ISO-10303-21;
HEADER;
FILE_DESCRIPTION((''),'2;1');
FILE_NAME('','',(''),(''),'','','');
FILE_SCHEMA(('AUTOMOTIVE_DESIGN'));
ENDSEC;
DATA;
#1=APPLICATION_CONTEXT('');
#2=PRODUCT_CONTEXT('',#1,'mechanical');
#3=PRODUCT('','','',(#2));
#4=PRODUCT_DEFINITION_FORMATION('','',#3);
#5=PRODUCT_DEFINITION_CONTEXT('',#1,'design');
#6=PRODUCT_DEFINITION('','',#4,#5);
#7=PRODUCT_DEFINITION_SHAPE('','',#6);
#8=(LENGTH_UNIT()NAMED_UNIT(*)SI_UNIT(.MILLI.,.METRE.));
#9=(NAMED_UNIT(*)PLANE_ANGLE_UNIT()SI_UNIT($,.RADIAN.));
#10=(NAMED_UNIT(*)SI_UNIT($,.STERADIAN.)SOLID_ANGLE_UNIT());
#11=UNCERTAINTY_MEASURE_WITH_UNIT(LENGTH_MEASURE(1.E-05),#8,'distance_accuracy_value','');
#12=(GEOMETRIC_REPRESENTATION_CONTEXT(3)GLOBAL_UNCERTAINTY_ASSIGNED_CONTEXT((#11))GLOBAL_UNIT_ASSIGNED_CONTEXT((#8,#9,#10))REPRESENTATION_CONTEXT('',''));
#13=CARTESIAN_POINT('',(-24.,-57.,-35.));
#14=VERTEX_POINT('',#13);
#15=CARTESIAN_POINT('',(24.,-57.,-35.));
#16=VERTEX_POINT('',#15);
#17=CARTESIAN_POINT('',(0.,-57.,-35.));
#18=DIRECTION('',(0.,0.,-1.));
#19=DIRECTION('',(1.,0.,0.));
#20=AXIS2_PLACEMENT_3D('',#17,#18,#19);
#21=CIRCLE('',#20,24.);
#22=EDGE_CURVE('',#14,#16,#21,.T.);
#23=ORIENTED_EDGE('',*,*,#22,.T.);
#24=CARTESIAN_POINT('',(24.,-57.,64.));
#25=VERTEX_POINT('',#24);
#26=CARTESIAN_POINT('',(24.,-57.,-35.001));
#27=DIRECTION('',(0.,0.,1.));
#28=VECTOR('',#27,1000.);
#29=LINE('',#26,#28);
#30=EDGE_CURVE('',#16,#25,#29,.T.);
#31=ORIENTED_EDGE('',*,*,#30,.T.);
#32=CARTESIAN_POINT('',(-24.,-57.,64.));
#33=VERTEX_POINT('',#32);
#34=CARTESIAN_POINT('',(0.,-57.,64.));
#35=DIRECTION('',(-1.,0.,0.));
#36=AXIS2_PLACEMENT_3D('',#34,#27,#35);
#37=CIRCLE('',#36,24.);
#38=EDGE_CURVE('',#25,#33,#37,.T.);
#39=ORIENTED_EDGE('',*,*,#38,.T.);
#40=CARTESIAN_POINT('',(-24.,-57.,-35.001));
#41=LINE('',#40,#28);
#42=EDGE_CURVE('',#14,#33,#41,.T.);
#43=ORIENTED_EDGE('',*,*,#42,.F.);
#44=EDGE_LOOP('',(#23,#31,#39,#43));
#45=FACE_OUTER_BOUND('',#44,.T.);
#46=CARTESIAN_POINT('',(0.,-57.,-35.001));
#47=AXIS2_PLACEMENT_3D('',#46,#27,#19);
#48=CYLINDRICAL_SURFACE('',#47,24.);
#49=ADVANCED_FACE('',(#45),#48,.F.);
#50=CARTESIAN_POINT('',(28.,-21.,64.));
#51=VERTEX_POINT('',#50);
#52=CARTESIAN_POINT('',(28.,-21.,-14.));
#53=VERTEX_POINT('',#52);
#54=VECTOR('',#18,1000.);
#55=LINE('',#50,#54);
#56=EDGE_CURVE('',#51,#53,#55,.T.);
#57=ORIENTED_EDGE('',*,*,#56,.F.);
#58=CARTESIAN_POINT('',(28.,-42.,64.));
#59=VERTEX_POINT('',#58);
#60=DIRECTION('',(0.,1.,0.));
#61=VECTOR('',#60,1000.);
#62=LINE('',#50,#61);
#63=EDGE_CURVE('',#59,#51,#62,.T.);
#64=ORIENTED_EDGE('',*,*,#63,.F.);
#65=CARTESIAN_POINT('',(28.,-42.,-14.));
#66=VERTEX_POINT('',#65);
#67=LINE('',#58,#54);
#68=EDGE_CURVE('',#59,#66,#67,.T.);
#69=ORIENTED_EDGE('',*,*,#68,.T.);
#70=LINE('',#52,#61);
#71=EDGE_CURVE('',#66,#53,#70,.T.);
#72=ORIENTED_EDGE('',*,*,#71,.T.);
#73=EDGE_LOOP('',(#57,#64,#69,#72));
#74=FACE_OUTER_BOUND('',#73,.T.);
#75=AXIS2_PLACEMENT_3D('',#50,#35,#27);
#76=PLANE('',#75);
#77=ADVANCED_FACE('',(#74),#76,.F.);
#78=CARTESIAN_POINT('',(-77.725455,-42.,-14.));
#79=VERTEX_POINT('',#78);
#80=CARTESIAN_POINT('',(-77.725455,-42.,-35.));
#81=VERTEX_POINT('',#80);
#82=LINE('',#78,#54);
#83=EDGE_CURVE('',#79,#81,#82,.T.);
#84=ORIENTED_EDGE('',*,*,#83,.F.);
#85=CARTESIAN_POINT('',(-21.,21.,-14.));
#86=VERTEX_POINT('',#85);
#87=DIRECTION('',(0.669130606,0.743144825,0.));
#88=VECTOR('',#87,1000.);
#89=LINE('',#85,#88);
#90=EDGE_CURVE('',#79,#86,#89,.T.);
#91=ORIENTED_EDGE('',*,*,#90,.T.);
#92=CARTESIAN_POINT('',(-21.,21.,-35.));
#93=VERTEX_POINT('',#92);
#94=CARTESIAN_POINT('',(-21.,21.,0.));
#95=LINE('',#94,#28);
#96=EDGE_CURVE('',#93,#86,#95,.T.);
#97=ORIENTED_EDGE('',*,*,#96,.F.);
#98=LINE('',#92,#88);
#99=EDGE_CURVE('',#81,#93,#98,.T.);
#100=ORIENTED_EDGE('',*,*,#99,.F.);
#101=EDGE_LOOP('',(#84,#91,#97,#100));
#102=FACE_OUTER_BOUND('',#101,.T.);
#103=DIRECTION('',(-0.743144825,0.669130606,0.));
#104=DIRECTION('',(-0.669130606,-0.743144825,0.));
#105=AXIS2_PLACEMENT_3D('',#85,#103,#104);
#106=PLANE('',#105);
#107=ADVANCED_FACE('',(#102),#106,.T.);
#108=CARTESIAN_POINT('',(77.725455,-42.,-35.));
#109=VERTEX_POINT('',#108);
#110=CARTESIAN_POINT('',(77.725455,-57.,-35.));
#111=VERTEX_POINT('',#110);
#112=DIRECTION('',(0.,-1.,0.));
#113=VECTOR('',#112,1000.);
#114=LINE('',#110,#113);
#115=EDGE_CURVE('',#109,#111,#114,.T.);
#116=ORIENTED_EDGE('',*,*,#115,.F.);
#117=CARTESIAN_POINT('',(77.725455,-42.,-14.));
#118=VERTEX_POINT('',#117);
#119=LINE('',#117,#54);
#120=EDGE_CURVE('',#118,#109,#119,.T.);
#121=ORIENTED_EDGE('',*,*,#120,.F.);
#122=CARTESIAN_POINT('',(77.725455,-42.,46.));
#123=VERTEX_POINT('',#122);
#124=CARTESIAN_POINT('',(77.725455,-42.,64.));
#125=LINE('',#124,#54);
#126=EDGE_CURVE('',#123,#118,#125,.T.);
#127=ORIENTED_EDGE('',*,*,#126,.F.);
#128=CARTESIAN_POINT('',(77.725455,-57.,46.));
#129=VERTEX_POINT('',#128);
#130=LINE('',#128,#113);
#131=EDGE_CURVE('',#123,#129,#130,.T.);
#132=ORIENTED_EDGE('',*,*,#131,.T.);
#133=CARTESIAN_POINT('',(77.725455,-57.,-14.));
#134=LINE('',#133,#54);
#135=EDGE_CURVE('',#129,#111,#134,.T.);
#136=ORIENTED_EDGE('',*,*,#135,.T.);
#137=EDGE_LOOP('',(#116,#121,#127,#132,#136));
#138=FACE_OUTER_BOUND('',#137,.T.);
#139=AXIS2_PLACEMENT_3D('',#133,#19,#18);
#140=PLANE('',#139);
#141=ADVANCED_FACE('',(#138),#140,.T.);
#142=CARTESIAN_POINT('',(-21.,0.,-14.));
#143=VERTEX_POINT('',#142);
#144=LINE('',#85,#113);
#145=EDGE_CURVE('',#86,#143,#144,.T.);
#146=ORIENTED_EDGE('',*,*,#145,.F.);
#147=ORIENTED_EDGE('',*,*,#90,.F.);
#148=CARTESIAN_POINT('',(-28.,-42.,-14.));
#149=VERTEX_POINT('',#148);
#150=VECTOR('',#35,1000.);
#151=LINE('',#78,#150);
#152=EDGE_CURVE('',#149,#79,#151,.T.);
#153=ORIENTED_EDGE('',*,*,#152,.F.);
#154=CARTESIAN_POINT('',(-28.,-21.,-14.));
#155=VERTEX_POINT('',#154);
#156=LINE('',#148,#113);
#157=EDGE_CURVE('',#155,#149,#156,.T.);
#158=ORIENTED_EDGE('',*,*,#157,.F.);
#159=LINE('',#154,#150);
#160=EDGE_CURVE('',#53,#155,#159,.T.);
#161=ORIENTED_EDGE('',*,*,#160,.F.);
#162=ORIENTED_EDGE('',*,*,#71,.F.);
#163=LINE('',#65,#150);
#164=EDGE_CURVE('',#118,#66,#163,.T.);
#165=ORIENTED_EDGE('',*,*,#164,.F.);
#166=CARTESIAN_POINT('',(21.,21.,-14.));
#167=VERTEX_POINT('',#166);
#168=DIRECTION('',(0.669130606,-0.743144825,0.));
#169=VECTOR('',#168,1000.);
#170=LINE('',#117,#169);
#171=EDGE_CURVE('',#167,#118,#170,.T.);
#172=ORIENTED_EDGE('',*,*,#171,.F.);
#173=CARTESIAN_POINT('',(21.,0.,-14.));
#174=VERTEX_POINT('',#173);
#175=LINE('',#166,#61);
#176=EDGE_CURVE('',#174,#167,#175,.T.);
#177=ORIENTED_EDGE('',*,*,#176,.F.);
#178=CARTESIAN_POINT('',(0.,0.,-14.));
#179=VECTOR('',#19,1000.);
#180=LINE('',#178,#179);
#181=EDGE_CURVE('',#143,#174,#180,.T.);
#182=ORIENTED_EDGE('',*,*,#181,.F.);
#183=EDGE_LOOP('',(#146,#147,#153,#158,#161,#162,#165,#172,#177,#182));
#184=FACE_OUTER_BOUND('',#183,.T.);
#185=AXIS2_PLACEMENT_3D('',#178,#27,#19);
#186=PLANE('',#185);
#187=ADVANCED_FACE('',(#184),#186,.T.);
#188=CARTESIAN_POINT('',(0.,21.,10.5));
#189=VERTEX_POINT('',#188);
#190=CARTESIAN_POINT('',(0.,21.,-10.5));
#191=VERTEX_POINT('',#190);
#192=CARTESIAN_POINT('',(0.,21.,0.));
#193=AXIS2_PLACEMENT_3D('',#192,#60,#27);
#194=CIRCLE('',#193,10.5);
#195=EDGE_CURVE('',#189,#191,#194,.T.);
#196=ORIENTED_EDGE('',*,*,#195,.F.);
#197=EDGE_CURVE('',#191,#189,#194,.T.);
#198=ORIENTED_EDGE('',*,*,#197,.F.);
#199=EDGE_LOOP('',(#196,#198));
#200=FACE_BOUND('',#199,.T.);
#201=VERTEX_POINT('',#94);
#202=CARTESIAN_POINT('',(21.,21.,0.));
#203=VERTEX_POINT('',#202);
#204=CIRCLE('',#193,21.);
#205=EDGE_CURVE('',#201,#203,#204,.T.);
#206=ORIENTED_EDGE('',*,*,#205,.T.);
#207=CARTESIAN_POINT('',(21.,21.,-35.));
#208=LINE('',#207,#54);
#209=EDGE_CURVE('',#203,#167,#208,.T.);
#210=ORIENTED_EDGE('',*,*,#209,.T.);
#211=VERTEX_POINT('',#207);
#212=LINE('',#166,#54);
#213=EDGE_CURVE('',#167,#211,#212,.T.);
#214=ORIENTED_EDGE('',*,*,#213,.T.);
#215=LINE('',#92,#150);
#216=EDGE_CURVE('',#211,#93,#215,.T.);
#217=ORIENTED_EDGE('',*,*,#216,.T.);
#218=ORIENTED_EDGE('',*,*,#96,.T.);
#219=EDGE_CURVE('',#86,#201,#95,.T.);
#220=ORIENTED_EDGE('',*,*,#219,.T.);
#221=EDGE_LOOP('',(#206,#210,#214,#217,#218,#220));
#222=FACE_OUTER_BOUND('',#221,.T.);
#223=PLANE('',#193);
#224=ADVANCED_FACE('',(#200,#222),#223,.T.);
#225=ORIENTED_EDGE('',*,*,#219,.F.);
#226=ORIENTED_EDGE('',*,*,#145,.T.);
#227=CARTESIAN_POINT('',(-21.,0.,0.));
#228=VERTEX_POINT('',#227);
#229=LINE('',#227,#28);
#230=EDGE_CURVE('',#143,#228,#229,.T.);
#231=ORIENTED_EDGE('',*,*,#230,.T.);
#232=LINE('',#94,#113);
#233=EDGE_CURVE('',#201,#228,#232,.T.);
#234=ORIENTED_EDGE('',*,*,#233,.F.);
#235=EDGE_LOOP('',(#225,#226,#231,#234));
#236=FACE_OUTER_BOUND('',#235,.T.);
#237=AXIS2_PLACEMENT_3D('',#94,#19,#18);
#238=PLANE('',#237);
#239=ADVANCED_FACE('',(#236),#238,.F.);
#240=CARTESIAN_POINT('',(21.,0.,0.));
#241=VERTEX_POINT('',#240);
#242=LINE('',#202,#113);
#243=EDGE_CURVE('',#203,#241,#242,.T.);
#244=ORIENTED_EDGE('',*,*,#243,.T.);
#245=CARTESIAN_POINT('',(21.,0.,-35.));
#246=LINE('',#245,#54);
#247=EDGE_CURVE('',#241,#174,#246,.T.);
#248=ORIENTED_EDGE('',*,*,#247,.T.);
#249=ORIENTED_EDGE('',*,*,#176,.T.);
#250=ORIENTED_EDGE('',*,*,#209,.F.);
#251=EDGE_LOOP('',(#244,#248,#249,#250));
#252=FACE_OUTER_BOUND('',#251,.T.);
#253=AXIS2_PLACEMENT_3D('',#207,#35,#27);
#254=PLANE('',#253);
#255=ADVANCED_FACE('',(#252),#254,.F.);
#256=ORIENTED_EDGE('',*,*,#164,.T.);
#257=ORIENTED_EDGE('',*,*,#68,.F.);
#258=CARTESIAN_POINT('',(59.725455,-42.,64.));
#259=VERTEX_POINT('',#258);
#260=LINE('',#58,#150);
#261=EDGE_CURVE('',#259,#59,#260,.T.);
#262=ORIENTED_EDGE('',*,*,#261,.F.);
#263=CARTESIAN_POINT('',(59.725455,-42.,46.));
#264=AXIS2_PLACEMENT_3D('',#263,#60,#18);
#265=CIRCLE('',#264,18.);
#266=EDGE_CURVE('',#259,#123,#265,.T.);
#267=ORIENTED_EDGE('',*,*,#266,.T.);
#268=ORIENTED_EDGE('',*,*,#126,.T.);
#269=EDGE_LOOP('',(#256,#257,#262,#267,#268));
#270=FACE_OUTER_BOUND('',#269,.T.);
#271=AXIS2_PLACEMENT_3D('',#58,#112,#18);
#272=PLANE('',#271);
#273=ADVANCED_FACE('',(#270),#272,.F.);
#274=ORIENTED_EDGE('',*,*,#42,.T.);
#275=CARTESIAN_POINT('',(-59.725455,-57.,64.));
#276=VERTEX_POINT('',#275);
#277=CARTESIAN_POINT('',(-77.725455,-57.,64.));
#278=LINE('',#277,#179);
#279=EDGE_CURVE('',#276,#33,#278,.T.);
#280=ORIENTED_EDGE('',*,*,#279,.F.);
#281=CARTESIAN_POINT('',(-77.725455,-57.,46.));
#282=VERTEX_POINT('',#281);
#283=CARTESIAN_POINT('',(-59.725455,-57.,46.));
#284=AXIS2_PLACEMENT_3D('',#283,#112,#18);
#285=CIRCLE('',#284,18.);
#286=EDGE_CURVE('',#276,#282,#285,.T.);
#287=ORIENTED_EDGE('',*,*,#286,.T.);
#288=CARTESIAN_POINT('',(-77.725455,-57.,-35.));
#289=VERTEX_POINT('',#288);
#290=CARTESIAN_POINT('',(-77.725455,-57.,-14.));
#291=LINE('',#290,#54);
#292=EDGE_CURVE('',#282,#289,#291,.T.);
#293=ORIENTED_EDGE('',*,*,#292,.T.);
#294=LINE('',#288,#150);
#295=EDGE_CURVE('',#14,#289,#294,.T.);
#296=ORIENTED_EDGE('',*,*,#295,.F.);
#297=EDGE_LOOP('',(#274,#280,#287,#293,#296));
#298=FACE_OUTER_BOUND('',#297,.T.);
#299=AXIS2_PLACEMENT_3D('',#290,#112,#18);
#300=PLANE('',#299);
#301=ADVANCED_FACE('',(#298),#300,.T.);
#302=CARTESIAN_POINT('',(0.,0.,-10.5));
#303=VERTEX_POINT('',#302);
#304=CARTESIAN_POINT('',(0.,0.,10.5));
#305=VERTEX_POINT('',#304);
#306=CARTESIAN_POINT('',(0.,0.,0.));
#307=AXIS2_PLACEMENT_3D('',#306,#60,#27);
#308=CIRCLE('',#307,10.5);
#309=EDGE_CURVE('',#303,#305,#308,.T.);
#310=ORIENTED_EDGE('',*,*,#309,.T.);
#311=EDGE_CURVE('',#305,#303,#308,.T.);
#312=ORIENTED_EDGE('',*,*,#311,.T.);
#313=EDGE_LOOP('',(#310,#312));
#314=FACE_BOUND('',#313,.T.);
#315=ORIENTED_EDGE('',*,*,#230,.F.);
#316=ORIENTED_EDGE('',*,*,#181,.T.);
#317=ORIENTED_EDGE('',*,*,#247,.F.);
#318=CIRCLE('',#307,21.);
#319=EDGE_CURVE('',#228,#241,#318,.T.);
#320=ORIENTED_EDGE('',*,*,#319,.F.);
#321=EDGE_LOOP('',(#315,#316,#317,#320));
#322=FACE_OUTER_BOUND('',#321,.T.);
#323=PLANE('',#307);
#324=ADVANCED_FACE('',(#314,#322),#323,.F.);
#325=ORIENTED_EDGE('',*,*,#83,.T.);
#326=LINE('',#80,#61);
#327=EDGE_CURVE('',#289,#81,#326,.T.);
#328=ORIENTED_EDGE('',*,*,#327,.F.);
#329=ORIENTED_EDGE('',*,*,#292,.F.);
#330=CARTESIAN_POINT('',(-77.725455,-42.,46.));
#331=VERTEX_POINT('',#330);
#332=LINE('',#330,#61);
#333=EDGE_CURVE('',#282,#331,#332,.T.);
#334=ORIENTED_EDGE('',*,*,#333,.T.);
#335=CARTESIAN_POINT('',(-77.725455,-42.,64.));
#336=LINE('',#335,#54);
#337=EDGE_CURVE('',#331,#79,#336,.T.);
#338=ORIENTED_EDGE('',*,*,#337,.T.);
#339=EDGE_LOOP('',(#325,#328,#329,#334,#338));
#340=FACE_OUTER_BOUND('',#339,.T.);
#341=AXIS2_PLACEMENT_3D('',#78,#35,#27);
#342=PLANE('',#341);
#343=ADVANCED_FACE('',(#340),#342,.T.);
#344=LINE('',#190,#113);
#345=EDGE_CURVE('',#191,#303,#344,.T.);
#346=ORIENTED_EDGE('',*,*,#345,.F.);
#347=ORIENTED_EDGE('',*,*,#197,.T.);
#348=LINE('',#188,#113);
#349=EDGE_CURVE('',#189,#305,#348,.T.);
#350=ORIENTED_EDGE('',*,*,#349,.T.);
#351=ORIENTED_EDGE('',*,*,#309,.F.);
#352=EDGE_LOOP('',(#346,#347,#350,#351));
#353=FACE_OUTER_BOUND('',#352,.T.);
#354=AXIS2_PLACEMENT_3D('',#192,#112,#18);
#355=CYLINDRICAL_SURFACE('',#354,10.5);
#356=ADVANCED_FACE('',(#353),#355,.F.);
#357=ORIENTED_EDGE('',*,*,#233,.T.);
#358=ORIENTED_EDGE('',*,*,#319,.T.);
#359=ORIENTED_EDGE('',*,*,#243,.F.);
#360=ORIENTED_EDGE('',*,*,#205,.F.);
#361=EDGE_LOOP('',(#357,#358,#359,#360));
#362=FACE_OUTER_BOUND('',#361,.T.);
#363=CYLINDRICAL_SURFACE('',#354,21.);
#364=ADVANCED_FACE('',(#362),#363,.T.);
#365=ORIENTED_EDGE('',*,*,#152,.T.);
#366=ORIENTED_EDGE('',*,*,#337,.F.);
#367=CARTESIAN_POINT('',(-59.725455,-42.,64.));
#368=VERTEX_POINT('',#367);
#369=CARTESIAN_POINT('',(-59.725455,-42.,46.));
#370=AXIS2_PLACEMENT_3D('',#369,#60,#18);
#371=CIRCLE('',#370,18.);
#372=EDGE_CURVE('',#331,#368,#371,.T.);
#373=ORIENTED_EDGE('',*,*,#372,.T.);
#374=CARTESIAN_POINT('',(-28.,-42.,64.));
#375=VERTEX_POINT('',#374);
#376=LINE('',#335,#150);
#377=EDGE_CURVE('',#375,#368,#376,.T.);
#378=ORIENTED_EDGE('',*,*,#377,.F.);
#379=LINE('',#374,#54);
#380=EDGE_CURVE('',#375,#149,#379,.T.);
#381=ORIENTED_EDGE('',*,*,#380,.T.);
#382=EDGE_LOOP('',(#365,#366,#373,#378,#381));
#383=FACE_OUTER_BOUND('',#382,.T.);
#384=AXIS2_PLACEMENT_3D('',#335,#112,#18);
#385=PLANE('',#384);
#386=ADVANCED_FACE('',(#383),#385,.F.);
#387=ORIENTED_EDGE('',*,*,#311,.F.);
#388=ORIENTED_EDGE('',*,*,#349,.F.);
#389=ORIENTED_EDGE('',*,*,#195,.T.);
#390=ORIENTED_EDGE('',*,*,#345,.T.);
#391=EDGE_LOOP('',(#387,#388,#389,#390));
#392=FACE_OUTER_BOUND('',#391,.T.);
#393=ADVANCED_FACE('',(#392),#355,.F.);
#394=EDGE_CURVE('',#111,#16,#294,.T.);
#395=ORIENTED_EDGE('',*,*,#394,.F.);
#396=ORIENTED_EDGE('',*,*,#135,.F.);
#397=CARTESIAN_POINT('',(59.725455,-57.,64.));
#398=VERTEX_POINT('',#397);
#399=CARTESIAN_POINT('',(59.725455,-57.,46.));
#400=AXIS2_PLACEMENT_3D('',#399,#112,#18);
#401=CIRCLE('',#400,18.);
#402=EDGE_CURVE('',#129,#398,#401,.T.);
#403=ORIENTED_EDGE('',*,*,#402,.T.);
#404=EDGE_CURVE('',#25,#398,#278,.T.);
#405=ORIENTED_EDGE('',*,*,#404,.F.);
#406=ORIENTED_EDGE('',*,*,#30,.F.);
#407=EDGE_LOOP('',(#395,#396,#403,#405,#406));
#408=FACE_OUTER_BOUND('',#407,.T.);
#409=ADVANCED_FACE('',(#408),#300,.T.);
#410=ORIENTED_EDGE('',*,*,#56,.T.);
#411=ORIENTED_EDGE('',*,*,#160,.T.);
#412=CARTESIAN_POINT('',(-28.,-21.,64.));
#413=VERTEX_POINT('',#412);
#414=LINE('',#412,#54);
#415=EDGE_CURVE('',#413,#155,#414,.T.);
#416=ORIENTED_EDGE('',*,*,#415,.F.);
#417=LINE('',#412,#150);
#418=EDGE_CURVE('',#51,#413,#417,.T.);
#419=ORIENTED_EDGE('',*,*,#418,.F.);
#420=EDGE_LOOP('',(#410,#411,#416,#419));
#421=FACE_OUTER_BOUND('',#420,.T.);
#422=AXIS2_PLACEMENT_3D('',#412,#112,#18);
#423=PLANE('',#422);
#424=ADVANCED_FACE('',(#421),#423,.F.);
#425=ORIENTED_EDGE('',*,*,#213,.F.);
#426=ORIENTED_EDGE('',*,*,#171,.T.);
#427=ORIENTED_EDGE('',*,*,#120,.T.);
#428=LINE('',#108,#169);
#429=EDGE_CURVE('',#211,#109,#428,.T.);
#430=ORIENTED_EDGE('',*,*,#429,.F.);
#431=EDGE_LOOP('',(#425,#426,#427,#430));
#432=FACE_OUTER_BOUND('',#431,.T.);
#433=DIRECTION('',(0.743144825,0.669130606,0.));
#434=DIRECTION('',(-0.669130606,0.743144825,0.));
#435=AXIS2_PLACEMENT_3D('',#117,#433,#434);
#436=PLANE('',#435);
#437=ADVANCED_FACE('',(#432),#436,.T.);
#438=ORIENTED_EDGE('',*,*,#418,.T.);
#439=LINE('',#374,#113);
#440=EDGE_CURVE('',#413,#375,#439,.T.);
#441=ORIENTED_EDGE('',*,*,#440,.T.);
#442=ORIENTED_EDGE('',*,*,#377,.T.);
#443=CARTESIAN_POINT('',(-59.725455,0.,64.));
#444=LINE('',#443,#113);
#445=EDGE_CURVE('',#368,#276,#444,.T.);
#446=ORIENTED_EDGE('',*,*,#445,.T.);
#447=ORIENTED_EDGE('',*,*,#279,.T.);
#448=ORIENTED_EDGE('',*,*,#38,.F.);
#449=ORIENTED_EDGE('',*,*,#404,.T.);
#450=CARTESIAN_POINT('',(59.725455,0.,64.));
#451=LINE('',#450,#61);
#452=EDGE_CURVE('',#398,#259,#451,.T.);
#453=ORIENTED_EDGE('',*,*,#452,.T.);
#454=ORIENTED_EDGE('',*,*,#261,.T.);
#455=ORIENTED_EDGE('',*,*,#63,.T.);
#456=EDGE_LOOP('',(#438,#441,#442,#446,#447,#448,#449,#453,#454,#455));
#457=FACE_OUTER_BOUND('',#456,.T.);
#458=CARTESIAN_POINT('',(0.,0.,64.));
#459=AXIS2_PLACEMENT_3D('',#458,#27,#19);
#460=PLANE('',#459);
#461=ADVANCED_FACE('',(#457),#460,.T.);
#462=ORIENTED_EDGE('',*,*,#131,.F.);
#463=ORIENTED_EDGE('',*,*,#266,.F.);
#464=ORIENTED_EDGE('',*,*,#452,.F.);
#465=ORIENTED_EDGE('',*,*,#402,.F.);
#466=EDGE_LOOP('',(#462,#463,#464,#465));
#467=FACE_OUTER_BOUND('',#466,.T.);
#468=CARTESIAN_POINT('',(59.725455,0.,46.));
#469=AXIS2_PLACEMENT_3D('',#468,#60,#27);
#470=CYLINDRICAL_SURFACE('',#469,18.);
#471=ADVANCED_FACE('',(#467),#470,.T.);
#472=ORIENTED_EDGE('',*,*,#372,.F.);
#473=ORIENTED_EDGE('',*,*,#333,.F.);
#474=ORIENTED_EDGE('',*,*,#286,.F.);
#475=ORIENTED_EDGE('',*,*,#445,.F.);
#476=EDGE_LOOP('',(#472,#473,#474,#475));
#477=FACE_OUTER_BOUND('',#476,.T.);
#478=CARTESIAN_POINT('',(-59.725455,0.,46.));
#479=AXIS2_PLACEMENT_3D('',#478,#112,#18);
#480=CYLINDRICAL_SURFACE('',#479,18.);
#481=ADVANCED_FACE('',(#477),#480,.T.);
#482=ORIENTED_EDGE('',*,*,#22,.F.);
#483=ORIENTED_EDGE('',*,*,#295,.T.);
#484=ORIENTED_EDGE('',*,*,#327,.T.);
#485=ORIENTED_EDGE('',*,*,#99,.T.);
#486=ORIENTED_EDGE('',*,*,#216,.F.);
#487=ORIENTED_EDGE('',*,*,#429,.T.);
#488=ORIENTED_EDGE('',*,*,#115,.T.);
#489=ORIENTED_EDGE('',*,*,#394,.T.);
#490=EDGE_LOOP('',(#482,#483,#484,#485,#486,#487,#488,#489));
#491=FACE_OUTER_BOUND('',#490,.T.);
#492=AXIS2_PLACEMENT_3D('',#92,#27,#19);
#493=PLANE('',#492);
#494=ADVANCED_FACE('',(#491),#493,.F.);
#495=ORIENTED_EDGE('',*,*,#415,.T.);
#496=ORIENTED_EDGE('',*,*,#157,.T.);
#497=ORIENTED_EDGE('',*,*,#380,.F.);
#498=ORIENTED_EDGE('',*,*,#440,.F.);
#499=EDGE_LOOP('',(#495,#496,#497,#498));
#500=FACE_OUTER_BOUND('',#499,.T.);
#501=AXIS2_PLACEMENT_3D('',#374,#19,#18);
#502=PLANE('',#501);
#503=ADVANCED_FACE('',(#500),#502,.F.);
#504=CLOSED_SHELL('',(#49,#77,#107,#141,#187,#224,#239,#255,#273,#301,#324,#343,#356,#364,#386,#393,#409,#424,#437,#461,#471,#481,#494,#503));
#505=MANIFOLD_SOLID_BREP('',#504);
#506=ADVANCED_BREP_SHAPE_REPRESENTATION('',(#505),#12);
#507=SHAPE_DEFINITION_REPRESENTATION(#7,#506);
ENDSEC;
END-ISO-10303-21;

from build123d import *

# Parameters (mm, degrees)
BASE_PLATE_SKETCH_R     = 10.5
BASE_PLATE_DEPTH        = 21
ANGLED_WEB_48DEG_DEPTH  = 21
UPRIGHT_BLOCK_DEPTH     = 78
CORNER_FILLETS_R18_R    = 18
HALF_ROUND_CUT_24_REACH = 140.171


with BuildPart() as part:
    # Base Plate Sketch → Base Plate (new body)
    with BuildSketch(Plane(origin=(0, 0, 0), x_dir=(1, 0, 0), z_dir=(0, 1, 0))):
        with BuildLine():
            Line((-21, 0), (-21, 35))
            Line((-21, 35), (21, 35))
            Line((21, 35), (21, 0))
            ThreePointArc((21, 0), (0, -21), (-21, 0))
        make_face()
        with Locations(Location((0, 0, 0), (0, 0, 90))):
            Circle(BASE_PLATE_SKETCH_R, mode=Mode.SUBTRACT)
    extrude(amount=BASE_PLATE_DEPTH)

    # Angled Web Sketch → Angled Web 48deg (add)
    with BuildSketch(Plane(origin=(0, 0, -35), x_dir=(-1, 0, 0), z_dir=(0, 0, -1))):
        Polygon((77.725454791, -42), (77.725454791, -57), (-77.725454791, -57), (-77.725454791, -42), (-21, 21), (21, 21), align=None)
    extrude(amount=-ANGLED_WEB_48DEG_DEPTH)

    # Upright Block Sketch → Upright Block (add)
    with BuildSketch(Plane.XY.offset(-14)):
        Polygon((-77.725454791, -42), (-28, -42), (-28, -21), (28, -21), (28, -42), (77.725454791, -42), (77.725454791, -57), (-77.725454791, -57), align=None)
    extrude(amount=UPRIGHT_BLOCK_DEPTH)

    # Corner Fillets R18
    corner_fillets_r18_edges = [part.edges().sort_by_distance(p)[0] for p in [
        (-77.725454791, -49.5, 64),
        (77.725454791, -49.5, 64),
    ]]
    fillet(corner_fillets_r18_edges, radius=CORNER_FILLETS_R18_R)

    # Half-Round Cut Sketch → Half-Round Cut Ø24 (cut, up to next)
    with BuildSketch(Plane.XY.offset(64), mode=Mode.PRIVATE) as half_round_cut_24_sk1:
        with BuildLine():
            Line((-24, -57), (24, -57))
            ThreePointArc((24, -57), (0, -33), (-24, -57))
        make_face()
    half_round_cut_24_tool1 = extrude(half_round_cut_24_sk1.sketch, amount=-HALF_ROUND_CUT_24_REACH, mode=Mode.PRIVATE) & part.part
    add(half_round_cut_24_tool1.solids().sort_by_distance((0, -46.814084, 64))[0], mode=Mode.SUBTRACT)


solid = part.part
